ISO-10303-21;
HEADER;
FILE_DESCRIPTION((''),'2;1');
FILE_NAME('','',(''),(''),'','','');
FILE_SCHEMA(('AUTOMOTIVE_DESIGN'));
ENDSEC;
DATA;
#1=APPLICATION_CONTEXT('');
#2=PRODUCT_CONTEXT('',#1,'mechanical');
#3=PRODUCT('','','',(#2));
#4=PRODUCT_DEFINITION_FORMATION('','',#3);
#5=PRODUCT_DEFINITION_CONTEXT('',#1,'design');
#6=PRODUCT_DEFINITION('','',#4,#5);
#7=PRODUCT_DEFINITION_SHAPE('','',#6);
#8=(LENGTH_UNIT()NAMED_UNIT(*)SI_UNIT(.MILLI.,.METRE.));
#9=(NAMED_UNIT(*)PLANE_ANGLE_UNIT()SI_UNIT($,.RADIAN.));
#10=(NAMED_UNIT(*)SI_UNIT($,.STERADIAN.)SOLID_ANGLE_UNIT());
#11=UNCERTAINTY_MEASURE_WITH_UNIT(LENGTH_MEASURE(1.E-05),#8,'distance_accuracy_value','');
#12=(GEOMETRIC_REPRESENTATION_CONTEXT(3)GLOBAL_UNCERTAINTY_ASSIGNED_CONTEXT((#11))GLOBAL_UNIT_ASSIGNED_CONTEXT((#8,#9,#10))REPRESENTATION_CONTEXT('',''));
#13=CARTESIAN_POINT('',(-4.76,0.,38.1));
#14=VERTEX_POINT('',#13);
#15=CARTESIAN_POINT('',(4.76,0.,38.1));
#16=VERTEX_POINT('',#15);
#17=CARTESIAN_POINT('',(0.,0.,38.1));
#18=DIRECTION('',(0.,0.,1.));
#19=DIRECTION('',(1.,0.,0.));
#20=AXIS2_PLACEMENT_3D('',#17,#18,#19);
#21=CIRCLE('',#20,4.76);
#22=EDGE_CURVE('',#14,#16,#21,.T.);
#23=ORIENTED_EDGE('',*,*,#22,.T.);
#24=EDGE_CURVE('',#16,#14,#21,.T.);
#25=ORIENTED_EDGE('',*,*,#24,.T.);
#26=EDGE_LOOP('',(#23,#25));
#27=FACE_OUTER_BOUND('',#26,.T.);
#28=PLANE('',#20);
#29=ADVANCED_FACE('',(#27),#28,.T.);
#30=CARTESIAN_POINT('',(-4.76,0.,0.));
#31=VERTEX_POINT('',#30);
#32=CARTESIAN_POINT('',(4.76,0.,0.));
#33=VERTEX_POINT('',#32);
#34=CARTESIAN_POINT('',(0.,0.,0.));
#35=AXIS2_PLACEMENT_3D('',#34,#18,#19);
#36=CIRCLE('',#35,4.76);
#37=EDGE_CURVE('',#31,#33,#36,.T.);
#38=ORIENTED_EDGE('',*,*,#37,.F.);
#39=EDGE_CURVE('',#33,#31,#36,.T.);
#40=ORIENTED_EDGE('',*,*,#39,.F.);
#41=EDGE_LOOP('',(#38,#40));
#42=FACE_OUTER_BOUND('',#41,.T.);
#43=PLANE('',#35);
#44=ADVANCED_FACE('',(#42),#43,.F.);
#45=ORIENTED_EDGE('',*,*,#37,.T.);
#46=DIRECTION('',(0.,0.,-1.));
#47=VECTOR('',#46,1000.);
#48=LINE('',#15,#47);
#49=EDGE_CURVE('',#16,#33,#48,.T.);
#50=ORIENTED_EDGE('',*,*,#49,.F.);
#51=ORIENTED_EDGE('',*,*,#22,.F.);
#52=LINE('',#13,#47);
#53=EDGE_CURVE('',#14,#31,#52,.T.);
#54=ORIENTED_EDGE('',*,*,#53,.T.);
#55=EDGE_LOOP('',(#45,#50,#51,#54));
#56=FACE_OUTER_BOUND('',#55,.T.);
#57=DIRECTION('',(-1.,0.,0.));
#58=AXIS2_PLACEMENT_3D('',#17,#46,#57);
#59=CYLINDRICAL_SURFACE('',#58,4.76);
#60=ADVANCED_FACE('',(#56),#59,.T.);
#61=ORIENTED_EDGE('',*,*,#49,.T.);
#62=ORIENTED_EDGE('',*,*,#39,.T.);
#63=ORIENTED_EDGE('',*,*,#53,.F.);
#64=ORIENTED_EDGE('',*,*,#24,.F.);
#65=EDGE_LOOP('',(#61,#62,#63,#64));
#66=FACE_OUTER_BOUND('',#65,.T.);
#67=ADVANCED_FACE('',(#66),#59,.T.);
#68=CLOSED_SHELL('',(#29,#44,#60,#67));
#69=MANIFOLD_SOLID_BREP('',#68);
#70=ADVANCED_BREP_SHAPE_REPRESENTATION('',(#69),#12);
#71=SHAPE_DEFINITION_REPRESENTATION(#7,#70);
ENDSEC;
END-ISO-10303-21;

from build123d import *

# Parameters (mm, degrees)
PIN_PROFILE_9_52_R   = 4.76
PIN_BODY_L38_1_DEPTH = 38.1


with BuildPart() as part:
    # Pin Profile Ø9.52 → Pin Body L38.1 (new body)
    with BuildSketch(Plane.XY):
        with Locations(Location((0, 0, 0), (0, 0, 180))):
            Circle(PIN_PROFILE_9_52_R)
    extrude(amount=PIN_BODY_L38_1_DEPTH)


solid = part.part
